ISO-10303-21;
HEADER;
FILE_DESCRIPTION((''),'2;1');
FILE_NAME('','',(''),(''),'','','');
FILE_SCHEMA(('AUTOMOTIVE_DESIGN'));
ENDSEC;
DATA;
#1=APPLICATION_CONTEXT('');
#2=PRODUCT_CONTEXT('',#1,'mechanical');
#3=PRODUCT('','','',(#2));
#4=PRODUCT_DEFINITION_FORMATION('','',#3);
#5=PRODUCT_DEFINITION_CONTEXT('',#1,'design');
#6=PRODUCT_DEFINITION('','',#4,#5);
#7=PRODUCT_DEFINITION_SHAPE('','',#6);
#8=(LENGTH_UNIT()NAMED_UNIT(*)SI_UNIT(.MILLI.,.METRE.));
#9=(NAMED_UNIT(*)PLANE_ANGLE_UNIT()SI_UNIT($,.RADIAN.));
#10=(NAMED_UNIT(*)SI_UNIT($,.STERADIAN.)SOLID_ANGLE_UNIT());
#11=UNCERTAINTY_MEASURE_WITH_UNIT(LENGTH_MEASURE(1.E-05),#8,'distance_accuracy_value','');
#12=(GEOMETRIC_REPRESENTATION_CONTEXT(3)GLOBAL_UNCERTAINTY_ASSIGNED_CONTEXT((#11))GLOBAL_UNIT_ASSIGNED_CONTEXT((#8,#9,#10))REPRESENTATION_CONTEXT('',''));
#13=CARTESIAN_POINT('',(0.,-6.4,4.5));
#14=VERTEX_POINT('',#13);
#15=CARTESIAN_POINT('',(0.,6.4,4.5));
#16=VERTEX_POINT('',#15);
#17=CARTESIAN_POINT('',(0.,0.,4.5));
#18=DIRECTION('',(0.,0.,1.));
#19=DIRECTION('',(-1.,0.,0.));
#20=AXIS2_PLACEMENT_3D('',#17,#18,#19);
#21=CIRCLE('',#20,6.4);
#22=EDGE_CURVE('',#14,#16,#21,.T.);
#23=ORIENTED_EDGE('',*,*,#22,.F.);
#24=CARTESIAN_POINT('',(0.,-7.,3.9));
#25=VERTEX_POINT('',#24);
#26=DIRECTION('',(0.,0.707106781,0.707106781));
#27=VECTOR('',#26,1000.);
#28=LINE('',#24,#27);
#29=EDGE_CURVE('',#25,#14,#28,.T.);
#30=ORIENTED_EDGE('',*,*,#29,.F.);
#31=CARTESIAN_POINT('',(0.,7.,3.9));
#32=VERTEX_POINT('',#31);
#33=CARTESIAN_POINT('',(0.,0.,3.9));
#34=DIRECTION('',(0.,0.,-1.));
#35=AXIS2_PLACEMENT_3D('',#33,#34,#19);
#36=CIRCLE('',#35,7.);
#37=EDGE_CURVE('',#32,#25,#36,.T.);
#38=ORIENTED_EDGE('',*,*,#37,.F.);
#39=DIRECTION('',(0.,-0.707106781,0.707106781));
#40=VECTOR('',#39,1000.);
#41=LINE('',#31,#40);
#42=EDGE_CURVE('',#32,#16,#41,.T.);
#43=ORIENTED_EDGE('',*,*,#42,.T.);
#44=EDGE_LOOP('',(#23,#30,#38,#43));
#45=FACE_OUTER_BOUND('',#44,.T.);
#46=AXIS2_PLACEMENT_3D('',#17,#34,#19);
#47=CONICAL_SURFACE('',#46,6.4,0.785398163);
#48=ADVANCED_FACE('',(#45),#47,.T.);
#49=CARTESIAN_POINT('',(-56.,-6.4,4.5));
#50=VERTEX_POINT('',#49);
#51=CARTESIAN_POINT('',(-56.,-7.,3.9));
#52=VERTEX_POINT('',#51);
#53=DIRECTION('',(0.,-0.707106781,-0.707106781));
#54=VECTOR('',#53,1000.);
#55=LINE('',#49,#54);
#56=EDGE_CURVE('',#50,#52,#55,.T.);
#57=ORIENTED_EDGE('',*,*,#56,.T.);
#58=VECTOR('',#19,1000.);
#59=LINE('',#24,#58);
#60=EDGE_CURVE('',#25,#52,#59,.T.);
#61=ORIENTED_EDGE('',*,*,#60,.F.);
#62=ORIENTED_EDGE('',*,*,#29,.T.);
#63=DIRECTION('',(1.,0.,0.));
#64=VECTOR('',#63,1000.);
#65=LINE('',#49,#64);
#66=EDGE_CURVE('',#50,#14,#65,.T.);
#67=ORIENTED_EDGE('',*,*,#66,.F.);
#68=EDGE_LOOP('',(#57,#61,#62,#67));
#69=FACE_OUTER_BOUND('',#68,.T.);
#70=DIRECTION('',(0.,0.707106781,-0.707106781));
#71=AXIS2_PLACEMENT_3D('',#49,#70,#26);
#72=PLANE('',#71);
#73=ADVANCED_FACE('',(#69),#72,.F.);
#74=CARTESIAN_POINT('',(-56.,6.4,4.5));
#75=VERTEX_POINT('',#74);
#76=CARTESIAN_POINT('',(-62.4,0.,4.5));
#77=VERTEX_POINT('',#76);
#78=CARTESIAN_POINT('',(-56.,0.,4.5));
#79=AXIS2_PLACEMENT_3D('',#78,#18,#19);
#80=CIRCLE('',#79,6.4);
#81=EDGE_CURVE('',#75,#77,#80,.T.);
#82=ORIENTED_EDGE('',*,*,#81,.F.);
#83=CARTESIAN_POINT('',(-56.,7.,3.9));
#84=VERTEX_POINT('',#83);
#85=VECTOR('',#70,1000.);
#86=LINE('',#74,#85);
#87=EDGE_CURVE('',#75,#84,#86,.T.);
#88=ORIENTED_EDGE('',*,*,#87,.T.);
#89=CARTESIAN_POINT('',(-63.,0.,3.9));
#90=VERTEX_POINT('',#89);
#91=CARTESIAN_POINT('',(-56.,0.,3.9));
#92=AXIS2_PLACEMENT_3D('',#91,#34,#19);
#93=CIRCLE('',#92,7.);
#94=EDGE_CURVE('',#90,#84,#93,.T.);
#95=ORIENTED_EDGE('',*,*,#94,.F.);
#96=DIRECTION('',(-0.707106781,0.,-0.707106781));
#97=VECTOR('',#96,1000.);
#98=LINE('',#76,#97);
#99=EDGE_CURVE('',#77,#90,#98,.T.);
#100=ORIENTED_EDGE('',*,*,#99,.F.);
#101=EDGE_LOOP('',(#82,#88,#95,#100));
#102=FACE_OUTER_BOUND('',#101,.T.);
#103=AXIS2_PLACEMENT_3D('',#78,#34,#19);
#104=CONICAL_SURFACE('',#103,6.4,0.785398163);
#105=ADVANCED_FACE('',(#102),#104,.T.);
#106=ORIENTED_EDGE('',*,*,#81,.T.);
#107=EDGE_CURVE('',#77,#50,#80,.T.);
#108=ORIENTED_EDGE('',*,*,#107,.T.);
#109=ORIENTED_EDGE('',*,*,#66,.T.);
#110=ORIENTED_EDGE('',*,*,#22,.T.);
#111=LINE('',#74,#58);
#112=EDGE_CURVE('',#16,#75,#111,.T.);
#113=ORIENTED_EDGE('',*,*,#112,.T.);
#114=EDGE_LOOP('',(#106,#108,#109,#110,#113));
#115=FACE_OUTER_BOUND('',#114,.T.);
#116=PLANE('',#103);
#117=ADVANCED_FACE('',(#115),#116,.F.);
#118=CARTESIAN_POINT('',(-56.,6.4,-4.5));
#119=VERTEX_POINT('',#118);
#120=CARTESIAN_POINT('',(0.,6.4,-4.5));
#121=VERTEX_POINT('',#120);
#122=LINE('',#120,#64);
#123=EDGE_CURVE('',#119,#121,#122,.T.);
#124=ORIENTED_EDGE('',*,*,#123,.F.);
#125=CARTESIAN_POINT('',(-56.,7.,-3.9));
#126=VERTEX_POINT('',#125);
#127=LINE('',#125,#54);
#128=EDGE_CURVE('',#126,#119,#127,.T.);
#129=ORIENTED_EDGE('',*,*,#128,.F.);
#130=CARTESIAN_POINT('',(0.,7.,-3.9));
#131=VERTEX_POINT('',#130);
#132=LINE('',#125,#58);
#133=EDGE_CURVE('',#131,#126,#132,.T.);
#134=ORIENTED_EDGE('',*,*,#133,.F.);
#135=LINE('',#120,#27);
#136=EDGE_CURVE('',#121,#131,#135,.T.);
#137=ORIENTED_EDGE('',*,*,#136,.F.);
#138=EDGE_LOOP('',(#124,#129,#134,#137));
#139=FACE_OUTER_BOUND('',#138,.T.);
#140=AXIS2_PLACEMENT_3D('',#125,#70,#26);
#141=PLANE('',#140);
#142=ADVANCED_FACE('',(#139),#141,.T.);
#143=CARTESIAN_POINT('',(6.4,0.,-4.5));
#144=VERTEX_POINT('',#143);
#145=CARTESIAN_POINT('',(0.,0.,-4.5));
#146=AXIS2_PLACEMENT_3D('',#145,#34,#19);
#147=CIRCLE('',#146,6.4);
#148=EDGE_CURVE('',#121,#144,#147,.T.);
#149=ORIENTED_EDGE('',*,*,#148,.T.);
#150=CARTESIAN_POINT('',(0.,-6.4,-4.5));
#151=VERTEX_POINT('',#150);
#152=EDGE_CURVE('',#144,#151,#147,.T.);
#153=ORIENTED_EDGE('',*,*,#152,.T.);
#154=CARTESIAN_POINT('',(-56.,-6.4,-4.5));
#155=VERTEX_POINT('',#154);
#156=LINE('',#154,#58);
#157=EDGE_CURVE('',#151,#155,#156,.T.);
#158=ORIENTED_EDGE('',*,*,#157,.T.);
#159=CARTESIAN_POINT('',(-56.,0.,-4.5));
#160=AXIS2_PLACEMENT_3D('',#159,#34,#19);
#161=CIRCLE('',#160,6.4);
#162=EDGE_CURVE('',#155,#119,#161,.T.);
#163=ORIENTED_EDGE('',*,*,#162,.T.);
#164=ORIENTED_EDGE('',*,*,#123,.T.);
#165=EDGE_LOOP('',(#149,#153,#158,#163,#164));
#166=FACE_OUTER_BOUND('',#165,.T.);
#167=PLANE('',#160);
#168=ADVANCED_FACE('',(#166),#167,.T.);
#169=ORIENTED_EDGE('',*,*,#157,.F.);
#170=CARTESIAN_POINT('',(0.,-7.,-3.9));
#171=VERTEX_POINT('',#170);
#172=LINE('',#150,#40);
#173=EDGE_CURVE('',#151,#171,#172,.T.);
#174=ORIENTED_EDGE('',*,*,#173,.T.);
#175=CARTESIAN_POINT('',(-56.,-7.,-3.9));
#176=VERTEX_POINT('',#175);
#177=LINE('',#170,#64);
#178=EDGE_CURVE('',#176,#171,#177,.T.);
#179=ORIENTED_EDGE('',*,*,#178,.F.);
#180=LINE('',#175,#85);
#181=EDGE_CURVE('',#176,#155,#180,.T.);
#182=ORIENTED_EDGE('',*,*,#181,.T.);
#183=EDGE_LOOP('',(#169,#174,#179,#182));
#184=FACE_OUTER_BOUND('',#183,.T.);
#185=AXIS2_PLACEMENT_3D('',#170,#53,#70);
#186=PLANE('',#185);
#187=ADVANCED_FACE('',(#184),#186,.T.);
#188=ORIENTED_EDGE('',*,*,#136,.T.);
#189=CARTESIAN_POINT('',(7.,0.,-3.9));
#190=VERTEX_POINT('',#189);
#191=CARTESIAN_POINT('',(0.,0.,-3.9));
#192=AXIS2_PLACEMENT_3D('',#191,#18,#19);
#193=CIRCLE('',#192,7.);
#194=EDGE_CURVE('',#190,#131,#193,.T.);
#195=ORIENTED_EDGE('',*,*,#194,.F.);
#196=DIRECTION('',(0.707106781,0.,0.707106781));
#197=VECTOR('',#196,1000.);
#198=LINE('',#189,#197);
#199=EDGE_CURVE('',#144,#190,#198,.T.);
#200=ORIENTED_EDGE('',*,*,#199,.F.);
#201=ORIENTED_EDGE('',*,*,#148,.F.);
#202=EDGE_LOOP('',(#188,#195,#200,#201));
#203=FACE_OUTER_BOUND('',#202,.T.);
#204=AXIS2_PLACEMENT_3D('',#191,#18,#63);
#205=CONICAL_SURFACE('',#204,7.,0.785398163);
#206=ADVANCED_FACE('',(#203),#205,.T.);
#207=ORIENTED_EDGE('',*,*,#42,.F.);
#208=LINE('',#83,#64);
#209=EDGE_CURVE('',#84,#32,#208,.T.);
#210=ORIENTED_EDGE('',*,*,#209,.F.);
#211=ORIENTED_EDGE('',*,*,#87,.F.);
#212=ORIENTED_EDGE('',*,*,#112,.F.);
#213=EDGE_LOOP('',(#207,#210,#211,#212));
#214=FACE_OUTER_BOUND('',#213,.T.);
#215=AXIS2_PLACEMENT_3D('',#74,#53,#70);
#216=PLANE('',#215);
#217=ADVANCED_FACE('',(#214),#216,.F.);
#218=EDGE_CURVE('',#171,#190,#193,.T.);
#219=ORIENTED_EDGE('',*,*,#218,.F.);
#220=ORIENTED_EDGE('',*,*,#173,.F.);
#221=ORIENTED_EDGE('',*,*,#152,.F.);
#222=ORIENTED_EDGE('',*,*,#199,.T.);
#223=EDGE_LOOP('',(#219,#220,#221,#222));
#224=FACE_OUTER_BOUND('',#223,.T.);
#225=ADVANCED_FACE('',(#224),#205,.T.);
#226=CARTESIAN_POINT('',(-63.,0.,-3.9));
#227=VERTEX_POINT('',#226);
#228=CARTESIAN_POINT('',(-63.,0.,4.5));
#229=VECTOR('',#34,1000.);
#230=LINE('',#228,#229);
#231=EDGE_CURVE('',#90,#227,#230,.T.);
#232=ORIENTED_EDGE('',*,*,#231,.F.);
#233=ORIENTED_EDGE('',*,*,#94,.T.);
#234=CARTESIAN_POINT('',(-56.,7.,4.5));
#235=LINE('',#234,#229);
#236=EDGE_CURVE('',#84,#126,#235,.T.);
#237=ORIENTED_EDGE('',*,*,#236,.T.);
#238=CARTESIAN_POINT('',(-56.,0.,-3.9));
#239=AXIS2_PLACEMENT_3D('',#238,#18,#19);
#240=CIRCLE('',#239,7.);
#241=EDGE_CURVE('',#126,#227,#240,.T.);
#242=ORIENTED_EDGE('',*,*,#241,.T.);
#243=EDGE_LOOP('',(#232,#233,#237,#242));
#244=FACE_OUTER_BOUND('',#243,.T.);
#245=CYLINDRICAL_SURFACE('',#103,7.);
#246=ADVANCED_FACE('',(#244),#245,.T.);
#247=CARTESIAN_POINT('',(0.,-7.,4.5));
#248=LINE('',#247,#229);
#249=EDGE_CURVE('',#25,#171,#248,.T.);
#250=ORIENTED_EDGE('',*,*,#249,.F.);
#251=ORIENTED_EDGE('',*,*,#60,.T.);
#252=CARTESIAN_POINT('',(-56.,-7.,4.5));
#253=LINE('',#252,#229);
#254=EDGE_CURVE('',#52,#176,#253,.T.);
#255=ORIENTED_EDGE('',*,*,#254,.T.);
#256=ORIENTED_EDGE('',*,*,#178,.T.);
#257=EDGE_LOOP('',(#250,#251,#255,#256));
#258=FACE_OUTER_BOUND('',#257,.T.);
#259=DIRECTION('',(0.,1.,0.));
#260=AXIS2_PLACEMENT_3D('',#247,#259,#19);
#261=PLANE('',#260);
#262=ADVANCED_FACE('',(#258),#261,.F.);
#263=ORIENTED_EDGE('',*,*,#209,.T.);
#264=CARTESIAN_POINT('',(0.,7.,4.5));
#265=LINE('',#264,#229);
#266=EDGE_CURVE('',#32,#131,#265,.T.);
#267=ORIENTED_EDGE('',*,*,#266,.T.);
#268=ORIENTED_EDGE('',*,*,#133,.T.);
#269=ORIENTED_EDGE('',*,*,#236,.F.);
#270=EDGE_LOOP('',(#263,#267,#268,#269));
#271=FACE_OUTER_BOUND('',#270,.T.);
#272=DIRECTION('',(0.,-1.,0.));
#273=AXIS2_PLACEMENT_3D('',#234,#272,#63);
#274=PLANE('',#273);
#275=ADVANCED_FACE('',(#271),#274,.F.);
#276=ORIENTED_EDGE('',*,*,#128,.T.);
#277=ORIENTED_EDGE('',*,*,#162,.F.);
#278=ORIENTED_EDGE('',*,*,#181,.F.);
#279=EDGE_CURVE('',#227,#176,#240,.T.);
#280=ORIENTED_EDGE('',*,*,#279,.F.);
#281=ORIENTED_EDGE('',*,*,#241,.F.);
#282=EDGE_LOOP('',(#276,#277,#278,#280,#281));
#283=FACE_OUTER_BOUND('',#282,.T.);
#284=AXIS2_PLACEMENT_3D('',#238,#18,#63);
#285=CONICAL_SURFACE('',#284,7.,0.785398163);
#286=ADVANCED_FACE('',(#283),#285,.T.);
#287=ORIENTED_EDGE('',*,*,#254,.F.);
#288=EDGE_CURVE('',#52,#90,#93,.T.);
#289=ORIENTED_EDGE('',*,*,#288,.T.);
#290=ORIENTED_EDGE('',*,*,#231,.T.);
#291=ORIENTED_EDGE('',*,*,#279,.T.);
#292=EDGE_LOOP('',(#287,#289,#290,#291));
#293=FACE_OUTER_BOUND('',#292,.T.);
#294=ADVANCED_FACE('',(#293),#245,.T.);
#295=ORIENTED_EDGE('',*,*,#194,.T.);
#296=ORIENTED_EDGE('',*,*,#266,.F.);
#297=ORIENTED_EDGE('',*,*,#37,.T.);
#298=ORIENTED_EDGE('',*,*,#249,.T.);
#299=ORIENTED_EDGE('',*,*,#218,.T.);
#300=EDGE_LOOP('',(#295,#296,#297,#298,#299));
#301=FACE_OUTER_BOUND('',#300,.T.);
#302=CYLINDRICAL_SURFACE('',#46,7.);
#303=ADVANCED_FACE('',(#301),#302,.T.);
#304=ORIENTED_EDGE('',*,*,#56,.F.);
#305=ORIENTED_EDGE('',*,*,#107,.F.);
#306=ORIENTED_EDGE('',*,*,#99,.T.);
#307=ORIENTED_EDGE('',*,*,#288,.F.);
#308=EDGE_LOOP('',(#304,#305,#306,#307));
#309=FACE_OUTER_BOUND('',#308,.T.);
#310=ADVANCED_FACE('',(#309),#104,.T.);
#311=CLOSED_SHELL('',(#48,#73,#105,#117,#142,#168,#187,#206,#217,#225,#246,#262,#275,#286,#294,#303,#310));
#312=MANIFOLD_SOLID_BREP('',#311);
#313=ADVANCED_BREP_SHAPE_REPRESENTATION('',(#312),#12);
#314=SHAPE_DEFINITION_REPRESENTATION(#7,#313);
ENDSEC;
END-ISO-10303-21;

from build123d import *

# Parameters (mm, degrees)
BASEKEY_DEPTH = 4.5
CHAMFER1_SIZE = 0.6


with BuildPart() as part:
    # Sketch1 → BaseKey (new, symmetric)
    with BuildSketch(Plane.XY):
        with BuildLine():
            Line((-56, 7), (0, 7))
            ThreePointArc((0, 7), (7, 0), (0, -7))
            Line((0, -7), (-56, -7))
            ThreePointArc((-56, -7), (-63, 0), (-56, 7))
        make_face()
    extrude(amount=BASEKEY_DEPTH, both=True)

    # Chamfer1
    chamfer1_edges = [part.edges().sort_by_distance(p)[0] for p in [
        (7, 0, 4.5),
        (-28, 7, 4.5),
        (-63, 0, 4.5),
        (-28, 7, -4.5),
        (7, 0, -4.5),
        (-28, -7, -4.5),
        (-63, 0, -4.5),
        (-28, -7, 4.5),
    ]]
    chamfer(chamfer1_edges, length=CHAMFER1_SIZE)


solid = part.part
